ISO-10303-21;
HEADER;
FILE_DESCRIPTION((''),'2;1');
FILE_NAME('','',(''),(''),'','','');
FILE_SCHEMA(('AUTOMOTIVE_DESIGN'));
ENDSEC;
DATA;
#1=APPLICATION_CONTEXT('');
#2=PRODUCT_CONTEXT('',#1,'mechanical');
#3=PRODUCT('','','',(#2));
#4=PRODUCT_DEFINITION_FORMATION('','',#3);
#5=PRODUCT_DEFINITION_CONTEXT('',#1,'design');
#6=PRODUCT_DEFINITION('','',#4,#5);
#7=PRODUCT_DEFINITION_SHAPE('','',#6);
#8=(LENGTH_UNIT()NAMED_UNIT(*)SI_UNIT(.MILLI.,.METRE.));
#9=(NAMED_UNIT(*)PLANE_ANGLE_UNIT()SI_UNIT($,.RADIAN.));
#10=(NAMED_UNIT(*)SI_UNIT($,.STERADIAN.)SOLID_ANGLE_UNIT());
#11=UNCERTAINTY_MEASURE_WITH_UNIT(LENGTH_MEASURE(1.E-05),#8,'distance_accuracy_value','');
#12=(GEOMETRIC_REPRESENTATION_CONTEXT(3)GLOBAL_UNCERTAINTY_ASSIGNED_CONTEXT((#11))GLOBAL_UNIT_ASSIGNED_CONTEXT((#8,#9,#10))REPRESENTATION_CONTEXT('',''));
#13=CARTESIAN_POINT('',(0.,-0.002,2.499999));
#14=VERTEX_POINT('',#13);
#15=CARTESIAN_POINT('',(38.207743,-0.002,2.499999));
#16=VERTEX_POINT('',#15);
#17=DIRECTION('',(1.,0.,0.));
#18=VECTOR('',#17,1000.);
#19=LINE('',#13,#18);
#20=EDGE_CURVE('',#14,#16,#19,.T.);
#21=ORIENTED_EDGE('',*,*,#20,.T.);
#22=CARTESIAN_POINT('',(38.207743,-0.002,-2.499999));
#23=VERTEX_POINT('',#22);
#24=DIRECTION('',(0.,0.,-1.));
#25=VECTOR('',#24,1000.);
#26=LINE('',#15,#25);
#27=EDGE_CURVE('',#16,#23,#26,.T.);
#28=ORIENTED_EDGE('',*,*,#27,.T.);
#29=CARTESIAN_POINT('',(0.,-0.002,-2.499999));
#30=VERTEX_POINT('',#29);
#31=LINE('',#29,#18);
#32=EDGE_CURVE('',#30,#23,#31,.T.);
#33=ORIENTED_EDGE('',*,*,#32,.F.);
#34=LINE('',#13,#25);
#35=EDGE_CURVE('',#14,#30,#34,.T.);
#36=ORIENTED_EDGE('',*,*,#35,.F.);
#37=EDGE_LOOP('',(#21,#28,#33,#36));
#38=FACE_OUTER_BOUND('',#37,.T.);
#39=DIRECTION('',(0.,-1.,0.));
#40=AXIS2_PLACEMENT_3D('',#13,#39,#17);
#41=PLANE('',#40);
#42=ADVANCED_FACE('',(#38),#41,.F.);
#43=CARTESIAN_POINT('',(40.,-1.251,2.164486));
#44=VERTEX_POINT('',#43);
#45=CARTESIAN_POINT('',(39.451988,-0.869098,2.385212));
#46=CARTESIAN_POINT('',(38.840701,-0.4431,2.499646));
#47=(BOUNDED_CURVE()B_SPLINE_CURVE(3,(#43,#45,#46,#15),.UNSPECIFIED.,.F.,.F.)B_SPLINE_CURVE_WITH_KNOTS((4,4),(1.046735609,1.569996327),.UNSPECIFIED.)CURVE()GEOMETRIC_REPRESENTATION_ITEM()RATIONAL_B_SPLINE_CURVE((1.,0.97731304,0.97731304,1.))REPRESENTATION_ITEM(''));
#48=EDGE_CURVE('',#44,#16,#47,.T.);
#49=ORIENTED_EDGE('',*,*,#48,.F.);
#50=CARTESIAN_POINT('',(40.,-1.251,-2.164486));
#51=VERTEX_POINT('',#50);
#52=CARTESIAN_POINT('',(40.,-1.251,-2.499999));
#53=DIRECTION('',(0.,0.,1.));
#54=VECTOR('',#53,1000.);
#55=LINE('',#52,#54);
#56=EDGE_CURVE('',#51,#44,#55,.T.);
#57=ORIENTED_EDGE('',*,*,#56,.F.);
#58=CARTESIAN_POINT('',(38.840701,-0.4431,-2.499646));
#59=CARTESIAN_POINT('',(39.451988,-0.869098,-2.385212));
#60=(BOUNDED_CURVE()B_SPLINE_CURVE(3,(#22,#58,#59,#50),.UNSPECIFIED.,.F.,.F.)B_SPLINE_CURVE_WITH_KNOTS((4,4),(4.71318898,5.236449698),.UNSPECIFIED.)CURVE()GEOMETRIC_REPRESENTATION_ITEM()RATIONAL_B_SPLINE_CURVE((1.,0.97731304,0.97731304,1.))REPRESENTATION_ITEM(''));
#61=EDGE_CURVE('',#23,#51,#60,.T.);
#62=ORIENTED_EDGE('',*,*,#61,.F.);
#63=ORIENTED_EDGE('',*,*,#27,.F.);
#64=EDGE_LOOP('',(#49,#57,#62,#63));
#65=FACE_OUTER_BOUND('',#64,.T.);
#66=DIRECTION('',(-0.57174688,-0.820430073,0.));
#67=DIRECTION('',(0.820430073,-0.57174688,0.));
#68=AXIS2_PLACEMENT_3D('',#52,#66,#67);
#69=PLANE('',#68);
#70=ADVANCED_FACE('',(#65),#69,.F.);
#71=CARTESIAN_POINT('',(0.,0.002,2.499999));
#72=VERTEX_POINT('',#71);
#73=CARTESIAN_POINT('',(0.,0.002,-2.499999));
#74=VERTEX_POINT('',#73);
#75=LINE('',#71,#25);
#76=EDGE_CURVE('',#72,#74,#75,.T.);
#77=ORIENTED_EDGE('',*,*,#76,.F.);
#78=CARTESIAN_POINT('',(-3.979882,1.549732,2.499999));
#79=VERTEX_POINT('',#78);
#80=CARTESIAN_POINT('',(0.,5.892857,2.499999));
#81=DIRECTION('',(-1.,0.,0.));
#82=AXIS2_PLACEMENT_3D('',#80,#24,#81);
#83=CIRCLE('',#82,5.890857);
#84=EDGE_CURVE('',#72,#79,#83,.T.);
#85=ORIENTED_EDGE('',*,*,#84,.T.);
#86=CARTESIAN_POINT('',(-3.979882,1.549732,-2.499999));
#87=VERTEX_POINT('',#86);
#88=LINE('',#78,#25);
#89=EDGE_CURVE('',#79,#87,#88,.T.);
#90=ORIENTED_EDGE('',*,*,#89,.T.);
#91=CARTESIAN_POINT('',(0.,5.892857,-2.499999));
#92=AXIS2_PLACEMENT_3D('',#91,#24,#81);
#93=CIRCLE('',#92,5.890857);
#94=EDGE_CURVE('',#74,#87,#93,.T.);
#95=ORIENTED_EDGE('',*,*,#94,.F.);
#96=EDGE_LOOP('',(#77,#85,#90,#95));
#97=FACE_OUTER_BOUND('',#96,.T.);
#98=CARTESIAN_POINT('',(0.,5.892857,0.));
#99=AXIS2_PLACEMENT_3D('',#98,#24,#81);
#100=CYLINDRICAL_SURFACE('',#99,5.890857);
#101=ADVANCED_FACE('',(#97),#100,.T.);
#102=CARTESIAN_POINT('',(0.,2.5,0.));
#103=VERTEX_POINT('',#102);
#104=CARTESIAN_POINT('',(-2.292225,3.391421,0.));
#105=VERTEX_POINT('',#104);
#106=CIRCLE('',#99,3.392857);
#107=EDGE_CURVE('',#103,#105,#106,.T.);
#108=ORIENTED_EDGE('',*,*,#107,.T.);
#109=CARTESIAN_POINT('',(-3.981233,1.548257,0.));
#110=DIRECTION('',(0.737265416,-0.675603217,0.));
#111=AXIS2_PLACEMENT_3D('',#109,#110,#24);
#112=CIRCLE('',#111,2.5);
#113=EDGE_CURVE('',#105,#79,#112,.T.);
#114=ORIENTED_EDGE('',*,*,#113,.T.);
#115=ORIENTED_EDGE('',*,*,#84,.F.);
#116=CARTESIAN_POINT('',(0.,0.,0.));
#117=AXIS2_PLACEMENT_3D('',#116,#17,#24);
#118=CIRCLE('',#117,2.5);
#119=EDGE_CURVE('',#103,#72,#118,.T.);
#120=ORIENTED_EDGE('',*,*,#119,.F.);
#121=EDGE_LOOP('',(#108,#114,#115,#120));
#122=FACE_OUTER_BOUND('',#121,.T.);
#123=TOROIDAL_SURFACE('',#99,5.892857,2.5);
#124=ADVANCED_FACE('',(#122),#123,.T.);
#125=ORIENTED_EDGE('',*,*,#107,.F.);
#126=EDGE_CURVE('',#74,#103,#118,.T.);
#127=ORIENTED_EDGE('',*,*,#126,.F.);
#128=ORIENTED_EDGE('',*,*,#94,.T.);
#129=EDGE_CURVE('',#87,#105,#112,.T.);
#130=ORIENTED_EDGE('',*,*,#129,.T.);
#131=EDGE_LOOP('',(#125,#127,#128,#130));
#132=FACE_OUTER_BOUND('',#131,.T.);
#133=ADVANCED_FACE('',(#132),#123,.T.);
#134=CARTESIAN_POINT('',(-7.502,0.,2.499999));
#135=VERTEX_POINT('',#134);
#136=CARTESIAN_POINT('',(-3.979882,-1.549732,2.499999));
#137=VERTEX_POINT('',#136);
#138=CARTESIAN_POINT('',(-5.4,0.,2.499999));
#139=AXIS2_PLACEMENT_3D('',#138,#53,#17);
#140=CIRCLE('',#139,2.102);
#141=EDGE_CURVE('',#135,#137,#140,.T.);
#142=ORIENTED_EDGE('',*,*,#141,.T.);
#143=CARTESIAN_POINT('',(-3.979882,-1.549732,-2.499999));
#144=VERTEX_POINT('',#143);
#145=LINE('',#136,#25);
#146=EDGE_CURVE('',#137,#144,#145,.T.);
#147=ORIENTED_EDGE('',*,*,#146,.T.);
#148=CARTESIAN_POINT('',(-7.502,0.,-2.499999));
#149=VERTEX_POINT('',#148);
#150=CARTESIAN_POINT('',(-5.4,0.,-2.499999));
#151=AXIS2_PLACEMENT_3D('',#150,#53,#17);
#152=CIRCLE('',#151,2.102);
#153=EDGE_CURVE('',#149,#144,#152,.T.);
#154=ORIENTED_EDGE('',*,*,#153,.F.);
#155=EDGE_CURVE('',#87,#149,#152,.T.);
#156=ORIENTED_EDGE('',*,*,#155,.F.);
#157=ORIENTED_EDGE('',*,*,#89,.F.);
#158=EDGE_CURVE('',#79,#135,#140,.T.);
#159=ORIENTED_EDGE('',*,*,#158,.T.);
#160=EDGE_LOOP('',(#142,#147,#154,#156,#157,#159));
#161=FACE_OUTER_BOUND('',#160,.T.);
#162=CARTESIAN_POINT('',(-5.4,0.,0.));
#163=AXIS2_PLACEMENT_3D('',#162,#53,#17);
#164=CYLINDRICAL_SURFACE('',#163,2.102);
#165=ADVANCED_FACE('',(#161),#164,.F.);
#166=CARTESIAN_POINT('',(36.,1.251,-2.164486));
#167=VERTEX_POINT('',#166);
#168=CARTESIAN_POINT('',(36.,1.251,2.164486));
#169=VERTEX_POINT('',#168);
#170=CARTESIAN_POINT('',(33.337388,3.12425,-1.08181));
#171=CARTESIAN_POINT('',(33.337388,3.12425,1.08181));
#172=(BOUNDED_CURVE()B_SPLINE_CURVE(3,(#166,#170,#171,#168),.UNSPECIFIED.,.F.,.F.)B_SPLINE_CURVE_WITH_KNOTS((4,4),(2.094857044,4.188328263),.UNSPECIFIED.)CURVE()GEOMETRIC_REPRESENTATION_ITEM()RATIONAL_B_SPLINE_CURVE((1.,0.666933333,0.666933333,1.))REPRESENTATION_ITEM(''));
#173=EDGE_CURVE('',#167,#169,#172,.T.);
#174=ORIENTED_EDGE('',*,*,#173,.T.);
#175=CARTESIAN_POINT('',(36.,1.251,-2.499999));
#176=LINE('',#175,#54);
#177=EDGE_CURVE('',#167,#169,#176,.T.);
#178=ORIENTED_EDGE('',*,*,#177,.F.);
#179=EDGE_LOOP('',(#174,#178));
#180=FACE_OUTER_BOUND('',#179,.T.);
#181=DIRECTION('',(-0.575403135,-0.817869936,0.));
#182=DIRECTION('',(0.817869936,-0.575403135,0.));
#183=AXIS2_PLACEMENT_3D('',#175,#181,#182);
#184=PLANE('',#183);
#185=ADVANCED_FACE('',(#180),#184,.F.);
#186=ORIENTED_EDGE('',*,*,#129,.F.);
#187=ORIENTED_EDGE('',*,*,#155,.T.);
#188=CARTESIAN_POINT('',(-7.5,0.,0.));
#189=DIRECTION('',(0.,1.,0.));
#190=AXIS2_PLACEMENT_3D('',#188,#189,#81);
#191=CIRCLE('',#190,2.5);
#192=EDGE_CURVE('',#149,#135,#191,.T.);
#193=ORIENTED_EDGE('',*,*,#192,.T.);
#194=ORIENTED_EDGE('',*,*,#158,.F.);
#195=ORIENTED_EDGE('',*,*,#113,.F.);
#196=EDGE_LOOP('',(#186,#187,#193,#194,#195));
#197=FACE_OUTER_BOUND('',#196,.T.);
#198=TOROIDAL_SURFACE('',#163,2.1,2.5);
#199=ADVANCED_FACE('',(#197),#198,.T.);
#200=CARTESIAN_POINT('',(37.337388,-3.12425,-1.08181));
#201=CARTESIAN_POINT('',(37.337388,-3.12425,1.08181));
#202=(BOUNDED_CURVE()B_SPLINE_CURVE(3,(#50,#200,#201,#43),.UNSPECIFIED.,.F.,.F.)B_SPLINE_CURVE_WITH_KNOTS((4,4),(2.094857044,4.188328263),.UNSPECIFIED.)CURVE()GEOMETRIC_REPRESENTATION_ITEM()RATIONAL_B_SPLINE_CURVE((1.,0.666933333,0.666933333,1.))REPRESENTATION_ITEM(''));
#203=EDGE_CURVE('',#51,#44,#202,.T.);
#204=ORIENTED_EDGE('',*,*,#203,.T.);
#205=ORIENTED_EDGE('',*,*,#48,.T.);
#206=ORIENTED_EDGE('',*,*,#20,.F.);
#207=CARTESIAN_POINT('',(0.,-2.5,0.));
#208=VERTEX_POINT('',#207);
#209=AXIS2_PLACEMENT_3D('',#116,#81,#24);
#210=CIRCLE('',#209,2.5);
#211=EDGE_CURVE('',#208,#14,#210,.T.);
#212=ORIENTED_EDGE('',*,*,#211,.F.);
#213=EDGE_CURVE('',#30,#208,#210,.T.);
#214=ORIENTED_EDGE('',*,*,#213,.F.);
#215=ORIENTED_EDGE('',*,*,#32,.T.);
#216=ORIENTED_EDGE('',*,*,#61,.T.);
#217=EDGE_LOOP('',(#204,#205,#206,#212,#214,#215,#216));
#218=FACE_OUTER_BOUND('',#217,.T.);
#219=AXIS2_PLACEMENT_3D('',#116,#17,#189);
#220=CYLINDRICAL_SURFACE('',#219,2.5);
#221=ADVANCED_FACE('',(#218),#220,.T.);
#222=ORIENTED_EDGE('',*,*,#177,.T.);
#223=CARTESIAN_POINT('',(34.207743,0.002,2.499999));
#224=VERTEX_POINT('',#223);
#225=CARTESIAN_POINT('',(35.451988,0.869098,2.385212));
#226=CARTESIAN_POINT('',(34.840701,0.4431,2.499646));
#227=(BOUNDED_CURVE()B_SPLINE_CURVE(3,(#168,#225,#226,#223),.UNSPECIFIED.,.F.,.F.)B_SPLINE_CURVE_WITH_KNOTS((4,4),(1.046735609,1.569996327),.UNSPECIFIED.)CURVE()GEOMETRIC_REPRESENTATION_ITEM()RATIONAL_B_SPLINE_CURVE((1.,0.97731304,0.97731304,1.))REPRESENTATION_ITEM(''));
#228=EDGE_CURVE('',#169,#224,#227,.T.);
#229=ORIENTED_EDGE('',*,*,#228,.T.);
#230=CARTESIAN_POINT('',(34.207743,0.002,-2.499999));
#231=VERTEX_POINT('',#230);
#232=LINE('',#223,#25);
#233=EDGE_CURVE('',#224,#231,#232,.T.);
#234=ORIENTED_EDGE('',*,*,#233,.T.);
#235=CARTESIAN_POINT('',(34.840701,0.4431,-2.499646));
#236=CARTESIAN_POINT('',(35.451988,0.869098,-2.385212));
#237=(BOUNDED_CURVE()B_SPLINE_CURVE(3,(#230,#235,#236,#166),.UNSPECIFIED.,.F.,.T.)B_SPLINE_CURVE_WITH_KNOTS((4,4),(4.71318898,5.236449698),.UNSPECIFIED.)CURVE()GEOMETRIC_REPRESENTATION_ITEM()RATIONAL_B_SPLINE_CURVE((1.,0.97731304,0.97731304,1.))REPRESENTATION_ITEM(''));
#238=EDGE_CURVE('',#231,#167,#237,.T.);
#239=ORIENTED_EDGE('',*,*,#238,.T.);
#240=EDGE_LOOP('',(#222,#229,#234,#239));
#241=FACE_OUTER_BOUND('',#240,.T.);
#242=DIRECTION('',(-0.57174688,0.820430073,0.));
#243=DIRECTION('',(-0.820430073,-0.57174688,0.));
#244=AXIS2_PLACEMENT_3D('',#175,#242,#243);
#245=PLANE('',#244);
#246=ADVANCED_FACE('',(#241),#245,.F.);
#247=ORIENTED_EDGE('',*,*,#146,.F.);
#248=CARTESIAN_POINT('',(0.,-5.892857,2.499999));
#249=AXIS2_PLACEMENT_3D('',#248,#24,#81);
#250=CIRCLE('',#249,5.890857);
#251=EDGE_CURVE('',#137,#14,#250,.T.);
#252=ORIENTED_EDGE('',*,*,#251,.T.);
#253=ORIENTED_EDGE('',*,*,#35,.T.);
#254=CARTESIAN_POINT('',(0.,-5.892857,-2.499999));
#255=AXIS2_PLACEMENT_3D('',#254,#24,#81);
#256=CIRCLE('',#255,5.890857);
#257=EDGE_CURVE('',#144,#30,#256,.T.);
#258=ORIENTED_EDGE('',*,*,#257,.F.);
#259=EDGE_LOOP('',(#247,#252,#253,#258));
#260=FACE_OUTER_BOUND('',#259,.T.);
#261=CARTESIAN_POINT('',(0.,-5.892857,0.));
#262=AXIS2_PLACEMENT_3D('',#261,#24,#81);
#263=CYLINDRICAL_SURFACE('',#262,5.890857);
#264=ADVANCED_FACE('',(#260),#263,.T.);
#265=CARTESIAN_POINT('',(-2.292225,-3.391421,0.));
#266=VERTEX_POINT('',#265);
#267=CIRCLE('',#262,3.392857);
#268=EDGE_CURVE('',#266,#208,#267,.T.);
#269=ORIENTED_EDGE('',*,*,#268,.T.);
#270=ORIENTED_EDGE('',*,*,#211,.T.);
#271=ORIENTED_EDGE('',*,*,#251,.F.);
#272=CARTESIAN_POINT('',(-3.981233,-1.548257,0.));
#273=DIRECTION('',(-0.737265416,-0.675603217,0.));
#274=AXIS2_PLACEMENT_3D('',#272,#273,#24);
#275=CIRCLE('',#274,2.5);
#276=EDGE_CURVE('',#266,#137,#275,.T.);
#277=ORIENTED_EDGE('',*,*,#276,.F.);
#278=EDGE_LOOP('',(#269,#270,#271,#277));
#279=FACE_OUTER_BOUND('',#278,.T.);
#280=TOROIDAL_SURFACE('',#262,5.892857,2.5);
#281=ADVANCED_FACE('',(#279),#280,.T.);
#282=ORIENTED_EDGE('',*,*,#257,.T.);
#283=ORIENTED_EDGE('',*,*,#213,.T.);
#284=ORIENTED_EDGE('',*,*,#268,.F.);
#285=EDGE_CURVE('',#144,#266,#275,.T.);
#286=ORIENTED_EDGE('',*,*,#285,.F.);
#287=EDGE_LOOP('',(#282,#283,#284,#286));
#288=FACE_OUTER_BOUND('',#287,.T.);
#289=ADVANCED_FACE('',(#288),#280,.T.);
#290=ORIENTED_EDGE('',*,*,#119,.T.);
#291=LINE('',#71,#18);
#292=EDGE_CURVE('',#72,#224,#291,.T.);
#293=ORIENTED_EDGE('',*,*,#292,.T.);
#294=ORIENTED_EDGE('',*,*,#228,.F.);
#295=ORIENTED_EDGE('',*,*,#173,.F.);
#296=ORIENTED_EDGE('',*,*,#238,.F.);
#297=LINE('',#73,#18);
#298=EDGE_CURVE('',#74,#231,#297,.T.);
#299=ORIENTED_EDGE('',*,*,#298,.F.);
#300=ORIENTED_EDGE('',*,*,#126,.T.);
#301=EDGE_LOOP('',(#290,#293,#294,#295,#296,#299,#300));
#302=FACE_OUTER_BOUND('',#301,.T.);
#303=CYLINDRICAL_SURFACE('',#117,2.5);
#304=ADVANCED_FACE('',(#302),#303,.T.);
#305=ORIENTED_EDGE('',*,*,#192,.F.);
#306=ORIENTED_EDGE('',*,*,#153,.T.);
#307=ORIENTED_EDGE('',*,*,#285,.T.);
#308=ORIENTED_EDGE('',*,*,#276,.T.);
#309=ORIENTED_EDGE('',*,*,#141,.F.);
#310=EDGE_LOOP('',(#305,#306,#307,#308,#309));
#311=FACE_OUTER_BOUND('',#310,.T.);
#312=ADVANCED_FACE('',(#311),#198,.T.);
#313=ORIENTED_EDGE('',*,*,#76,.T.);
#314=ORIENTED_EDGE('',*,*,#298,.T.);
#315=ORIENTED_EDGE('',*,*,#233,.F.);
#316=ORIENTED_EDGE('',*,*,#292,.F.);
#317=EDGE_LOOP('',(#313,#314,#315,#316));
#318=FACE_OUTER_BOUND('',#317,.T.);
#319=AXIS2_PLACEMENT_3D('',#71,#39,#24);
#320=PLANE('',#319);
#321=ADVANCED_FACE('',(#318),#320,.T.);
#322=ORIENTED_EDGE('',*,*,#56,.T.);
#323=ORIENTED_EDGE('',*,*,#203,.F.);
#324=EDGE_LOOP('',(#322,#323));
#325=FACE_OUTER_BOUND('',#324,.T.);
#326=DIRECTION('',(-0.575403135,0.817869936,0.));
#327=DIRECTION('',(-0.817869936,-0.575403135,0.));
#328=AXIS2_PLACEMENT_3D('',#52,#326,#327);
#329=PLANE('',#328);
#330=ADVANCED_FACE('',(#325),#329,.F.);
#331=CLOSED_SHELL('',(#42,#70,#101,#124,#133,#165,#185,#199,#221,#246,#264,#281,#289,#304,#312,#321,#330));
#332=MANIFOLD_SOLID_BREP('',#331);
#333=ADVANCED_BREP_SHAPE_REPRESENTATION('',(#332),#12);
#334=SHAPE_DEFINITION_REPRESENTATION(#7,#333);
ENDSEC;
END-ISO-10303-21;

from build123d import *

# Parameters (mm, degrees)
CONECUT_DEPTH      = 41.341170006
CONECUT_DEPTH_BACK = 41.341170006


with BuildPart() as part:
    # Body: sweep along a path in Sketch2
    with BuildLine(Plane.XY) as body_path:
        Line((36, 2.5), (0, 2.5))
        ThreePointArc((0, 2.5), (-1.229728386, 2.730698436), (-2.292225201, 3.391420912))
        ThreePointArc((-2.292225201, 3.391420912), (-10, 0), (-2.292225201, -3.391420912))
        ThreePointArc((-2.292225201, -3.391420912), (-1.229728386, -2.730698436), (0, -2.5))
        Line((0, -2.5), (40, -2.5))
    # Sketch1 → Body (sweep)
    with BuildSketch(Plane(origin=(36, 0, 0), x_dir=(0, 0, -1), z_dir=(1, 0, 0))):
        with BuildLine():
            Line((-2.4999992, 0.002), (2.4999992, 0.002))
            ThreePointArc((2.4999992, 0.002), (0, 2.5), (-2.4999992, 0.002))
        make_face()
    sweep(path=body_path.line)

    # Sketch3 → ConeCut (cut, two sides: drawn at the far end of the back side and taken through both)
    with BuildSketch(Plane.XY.offset(-CONECUT_DEPTH_BACK)):
        Polygon((36, 1.251), (34.210475082, 2.51), (40.01, 2.51), (40.01, -2.51), (38.210475082, -2.51), (40, -1.251), (38.204873421, 0), (34.204873421, 0), align=None)
    extrude(amount=CONECUT_DEPTH + CONECUT_DEPTH_BACK, mode=Mode.SUBTRACT)


solid = part.part
